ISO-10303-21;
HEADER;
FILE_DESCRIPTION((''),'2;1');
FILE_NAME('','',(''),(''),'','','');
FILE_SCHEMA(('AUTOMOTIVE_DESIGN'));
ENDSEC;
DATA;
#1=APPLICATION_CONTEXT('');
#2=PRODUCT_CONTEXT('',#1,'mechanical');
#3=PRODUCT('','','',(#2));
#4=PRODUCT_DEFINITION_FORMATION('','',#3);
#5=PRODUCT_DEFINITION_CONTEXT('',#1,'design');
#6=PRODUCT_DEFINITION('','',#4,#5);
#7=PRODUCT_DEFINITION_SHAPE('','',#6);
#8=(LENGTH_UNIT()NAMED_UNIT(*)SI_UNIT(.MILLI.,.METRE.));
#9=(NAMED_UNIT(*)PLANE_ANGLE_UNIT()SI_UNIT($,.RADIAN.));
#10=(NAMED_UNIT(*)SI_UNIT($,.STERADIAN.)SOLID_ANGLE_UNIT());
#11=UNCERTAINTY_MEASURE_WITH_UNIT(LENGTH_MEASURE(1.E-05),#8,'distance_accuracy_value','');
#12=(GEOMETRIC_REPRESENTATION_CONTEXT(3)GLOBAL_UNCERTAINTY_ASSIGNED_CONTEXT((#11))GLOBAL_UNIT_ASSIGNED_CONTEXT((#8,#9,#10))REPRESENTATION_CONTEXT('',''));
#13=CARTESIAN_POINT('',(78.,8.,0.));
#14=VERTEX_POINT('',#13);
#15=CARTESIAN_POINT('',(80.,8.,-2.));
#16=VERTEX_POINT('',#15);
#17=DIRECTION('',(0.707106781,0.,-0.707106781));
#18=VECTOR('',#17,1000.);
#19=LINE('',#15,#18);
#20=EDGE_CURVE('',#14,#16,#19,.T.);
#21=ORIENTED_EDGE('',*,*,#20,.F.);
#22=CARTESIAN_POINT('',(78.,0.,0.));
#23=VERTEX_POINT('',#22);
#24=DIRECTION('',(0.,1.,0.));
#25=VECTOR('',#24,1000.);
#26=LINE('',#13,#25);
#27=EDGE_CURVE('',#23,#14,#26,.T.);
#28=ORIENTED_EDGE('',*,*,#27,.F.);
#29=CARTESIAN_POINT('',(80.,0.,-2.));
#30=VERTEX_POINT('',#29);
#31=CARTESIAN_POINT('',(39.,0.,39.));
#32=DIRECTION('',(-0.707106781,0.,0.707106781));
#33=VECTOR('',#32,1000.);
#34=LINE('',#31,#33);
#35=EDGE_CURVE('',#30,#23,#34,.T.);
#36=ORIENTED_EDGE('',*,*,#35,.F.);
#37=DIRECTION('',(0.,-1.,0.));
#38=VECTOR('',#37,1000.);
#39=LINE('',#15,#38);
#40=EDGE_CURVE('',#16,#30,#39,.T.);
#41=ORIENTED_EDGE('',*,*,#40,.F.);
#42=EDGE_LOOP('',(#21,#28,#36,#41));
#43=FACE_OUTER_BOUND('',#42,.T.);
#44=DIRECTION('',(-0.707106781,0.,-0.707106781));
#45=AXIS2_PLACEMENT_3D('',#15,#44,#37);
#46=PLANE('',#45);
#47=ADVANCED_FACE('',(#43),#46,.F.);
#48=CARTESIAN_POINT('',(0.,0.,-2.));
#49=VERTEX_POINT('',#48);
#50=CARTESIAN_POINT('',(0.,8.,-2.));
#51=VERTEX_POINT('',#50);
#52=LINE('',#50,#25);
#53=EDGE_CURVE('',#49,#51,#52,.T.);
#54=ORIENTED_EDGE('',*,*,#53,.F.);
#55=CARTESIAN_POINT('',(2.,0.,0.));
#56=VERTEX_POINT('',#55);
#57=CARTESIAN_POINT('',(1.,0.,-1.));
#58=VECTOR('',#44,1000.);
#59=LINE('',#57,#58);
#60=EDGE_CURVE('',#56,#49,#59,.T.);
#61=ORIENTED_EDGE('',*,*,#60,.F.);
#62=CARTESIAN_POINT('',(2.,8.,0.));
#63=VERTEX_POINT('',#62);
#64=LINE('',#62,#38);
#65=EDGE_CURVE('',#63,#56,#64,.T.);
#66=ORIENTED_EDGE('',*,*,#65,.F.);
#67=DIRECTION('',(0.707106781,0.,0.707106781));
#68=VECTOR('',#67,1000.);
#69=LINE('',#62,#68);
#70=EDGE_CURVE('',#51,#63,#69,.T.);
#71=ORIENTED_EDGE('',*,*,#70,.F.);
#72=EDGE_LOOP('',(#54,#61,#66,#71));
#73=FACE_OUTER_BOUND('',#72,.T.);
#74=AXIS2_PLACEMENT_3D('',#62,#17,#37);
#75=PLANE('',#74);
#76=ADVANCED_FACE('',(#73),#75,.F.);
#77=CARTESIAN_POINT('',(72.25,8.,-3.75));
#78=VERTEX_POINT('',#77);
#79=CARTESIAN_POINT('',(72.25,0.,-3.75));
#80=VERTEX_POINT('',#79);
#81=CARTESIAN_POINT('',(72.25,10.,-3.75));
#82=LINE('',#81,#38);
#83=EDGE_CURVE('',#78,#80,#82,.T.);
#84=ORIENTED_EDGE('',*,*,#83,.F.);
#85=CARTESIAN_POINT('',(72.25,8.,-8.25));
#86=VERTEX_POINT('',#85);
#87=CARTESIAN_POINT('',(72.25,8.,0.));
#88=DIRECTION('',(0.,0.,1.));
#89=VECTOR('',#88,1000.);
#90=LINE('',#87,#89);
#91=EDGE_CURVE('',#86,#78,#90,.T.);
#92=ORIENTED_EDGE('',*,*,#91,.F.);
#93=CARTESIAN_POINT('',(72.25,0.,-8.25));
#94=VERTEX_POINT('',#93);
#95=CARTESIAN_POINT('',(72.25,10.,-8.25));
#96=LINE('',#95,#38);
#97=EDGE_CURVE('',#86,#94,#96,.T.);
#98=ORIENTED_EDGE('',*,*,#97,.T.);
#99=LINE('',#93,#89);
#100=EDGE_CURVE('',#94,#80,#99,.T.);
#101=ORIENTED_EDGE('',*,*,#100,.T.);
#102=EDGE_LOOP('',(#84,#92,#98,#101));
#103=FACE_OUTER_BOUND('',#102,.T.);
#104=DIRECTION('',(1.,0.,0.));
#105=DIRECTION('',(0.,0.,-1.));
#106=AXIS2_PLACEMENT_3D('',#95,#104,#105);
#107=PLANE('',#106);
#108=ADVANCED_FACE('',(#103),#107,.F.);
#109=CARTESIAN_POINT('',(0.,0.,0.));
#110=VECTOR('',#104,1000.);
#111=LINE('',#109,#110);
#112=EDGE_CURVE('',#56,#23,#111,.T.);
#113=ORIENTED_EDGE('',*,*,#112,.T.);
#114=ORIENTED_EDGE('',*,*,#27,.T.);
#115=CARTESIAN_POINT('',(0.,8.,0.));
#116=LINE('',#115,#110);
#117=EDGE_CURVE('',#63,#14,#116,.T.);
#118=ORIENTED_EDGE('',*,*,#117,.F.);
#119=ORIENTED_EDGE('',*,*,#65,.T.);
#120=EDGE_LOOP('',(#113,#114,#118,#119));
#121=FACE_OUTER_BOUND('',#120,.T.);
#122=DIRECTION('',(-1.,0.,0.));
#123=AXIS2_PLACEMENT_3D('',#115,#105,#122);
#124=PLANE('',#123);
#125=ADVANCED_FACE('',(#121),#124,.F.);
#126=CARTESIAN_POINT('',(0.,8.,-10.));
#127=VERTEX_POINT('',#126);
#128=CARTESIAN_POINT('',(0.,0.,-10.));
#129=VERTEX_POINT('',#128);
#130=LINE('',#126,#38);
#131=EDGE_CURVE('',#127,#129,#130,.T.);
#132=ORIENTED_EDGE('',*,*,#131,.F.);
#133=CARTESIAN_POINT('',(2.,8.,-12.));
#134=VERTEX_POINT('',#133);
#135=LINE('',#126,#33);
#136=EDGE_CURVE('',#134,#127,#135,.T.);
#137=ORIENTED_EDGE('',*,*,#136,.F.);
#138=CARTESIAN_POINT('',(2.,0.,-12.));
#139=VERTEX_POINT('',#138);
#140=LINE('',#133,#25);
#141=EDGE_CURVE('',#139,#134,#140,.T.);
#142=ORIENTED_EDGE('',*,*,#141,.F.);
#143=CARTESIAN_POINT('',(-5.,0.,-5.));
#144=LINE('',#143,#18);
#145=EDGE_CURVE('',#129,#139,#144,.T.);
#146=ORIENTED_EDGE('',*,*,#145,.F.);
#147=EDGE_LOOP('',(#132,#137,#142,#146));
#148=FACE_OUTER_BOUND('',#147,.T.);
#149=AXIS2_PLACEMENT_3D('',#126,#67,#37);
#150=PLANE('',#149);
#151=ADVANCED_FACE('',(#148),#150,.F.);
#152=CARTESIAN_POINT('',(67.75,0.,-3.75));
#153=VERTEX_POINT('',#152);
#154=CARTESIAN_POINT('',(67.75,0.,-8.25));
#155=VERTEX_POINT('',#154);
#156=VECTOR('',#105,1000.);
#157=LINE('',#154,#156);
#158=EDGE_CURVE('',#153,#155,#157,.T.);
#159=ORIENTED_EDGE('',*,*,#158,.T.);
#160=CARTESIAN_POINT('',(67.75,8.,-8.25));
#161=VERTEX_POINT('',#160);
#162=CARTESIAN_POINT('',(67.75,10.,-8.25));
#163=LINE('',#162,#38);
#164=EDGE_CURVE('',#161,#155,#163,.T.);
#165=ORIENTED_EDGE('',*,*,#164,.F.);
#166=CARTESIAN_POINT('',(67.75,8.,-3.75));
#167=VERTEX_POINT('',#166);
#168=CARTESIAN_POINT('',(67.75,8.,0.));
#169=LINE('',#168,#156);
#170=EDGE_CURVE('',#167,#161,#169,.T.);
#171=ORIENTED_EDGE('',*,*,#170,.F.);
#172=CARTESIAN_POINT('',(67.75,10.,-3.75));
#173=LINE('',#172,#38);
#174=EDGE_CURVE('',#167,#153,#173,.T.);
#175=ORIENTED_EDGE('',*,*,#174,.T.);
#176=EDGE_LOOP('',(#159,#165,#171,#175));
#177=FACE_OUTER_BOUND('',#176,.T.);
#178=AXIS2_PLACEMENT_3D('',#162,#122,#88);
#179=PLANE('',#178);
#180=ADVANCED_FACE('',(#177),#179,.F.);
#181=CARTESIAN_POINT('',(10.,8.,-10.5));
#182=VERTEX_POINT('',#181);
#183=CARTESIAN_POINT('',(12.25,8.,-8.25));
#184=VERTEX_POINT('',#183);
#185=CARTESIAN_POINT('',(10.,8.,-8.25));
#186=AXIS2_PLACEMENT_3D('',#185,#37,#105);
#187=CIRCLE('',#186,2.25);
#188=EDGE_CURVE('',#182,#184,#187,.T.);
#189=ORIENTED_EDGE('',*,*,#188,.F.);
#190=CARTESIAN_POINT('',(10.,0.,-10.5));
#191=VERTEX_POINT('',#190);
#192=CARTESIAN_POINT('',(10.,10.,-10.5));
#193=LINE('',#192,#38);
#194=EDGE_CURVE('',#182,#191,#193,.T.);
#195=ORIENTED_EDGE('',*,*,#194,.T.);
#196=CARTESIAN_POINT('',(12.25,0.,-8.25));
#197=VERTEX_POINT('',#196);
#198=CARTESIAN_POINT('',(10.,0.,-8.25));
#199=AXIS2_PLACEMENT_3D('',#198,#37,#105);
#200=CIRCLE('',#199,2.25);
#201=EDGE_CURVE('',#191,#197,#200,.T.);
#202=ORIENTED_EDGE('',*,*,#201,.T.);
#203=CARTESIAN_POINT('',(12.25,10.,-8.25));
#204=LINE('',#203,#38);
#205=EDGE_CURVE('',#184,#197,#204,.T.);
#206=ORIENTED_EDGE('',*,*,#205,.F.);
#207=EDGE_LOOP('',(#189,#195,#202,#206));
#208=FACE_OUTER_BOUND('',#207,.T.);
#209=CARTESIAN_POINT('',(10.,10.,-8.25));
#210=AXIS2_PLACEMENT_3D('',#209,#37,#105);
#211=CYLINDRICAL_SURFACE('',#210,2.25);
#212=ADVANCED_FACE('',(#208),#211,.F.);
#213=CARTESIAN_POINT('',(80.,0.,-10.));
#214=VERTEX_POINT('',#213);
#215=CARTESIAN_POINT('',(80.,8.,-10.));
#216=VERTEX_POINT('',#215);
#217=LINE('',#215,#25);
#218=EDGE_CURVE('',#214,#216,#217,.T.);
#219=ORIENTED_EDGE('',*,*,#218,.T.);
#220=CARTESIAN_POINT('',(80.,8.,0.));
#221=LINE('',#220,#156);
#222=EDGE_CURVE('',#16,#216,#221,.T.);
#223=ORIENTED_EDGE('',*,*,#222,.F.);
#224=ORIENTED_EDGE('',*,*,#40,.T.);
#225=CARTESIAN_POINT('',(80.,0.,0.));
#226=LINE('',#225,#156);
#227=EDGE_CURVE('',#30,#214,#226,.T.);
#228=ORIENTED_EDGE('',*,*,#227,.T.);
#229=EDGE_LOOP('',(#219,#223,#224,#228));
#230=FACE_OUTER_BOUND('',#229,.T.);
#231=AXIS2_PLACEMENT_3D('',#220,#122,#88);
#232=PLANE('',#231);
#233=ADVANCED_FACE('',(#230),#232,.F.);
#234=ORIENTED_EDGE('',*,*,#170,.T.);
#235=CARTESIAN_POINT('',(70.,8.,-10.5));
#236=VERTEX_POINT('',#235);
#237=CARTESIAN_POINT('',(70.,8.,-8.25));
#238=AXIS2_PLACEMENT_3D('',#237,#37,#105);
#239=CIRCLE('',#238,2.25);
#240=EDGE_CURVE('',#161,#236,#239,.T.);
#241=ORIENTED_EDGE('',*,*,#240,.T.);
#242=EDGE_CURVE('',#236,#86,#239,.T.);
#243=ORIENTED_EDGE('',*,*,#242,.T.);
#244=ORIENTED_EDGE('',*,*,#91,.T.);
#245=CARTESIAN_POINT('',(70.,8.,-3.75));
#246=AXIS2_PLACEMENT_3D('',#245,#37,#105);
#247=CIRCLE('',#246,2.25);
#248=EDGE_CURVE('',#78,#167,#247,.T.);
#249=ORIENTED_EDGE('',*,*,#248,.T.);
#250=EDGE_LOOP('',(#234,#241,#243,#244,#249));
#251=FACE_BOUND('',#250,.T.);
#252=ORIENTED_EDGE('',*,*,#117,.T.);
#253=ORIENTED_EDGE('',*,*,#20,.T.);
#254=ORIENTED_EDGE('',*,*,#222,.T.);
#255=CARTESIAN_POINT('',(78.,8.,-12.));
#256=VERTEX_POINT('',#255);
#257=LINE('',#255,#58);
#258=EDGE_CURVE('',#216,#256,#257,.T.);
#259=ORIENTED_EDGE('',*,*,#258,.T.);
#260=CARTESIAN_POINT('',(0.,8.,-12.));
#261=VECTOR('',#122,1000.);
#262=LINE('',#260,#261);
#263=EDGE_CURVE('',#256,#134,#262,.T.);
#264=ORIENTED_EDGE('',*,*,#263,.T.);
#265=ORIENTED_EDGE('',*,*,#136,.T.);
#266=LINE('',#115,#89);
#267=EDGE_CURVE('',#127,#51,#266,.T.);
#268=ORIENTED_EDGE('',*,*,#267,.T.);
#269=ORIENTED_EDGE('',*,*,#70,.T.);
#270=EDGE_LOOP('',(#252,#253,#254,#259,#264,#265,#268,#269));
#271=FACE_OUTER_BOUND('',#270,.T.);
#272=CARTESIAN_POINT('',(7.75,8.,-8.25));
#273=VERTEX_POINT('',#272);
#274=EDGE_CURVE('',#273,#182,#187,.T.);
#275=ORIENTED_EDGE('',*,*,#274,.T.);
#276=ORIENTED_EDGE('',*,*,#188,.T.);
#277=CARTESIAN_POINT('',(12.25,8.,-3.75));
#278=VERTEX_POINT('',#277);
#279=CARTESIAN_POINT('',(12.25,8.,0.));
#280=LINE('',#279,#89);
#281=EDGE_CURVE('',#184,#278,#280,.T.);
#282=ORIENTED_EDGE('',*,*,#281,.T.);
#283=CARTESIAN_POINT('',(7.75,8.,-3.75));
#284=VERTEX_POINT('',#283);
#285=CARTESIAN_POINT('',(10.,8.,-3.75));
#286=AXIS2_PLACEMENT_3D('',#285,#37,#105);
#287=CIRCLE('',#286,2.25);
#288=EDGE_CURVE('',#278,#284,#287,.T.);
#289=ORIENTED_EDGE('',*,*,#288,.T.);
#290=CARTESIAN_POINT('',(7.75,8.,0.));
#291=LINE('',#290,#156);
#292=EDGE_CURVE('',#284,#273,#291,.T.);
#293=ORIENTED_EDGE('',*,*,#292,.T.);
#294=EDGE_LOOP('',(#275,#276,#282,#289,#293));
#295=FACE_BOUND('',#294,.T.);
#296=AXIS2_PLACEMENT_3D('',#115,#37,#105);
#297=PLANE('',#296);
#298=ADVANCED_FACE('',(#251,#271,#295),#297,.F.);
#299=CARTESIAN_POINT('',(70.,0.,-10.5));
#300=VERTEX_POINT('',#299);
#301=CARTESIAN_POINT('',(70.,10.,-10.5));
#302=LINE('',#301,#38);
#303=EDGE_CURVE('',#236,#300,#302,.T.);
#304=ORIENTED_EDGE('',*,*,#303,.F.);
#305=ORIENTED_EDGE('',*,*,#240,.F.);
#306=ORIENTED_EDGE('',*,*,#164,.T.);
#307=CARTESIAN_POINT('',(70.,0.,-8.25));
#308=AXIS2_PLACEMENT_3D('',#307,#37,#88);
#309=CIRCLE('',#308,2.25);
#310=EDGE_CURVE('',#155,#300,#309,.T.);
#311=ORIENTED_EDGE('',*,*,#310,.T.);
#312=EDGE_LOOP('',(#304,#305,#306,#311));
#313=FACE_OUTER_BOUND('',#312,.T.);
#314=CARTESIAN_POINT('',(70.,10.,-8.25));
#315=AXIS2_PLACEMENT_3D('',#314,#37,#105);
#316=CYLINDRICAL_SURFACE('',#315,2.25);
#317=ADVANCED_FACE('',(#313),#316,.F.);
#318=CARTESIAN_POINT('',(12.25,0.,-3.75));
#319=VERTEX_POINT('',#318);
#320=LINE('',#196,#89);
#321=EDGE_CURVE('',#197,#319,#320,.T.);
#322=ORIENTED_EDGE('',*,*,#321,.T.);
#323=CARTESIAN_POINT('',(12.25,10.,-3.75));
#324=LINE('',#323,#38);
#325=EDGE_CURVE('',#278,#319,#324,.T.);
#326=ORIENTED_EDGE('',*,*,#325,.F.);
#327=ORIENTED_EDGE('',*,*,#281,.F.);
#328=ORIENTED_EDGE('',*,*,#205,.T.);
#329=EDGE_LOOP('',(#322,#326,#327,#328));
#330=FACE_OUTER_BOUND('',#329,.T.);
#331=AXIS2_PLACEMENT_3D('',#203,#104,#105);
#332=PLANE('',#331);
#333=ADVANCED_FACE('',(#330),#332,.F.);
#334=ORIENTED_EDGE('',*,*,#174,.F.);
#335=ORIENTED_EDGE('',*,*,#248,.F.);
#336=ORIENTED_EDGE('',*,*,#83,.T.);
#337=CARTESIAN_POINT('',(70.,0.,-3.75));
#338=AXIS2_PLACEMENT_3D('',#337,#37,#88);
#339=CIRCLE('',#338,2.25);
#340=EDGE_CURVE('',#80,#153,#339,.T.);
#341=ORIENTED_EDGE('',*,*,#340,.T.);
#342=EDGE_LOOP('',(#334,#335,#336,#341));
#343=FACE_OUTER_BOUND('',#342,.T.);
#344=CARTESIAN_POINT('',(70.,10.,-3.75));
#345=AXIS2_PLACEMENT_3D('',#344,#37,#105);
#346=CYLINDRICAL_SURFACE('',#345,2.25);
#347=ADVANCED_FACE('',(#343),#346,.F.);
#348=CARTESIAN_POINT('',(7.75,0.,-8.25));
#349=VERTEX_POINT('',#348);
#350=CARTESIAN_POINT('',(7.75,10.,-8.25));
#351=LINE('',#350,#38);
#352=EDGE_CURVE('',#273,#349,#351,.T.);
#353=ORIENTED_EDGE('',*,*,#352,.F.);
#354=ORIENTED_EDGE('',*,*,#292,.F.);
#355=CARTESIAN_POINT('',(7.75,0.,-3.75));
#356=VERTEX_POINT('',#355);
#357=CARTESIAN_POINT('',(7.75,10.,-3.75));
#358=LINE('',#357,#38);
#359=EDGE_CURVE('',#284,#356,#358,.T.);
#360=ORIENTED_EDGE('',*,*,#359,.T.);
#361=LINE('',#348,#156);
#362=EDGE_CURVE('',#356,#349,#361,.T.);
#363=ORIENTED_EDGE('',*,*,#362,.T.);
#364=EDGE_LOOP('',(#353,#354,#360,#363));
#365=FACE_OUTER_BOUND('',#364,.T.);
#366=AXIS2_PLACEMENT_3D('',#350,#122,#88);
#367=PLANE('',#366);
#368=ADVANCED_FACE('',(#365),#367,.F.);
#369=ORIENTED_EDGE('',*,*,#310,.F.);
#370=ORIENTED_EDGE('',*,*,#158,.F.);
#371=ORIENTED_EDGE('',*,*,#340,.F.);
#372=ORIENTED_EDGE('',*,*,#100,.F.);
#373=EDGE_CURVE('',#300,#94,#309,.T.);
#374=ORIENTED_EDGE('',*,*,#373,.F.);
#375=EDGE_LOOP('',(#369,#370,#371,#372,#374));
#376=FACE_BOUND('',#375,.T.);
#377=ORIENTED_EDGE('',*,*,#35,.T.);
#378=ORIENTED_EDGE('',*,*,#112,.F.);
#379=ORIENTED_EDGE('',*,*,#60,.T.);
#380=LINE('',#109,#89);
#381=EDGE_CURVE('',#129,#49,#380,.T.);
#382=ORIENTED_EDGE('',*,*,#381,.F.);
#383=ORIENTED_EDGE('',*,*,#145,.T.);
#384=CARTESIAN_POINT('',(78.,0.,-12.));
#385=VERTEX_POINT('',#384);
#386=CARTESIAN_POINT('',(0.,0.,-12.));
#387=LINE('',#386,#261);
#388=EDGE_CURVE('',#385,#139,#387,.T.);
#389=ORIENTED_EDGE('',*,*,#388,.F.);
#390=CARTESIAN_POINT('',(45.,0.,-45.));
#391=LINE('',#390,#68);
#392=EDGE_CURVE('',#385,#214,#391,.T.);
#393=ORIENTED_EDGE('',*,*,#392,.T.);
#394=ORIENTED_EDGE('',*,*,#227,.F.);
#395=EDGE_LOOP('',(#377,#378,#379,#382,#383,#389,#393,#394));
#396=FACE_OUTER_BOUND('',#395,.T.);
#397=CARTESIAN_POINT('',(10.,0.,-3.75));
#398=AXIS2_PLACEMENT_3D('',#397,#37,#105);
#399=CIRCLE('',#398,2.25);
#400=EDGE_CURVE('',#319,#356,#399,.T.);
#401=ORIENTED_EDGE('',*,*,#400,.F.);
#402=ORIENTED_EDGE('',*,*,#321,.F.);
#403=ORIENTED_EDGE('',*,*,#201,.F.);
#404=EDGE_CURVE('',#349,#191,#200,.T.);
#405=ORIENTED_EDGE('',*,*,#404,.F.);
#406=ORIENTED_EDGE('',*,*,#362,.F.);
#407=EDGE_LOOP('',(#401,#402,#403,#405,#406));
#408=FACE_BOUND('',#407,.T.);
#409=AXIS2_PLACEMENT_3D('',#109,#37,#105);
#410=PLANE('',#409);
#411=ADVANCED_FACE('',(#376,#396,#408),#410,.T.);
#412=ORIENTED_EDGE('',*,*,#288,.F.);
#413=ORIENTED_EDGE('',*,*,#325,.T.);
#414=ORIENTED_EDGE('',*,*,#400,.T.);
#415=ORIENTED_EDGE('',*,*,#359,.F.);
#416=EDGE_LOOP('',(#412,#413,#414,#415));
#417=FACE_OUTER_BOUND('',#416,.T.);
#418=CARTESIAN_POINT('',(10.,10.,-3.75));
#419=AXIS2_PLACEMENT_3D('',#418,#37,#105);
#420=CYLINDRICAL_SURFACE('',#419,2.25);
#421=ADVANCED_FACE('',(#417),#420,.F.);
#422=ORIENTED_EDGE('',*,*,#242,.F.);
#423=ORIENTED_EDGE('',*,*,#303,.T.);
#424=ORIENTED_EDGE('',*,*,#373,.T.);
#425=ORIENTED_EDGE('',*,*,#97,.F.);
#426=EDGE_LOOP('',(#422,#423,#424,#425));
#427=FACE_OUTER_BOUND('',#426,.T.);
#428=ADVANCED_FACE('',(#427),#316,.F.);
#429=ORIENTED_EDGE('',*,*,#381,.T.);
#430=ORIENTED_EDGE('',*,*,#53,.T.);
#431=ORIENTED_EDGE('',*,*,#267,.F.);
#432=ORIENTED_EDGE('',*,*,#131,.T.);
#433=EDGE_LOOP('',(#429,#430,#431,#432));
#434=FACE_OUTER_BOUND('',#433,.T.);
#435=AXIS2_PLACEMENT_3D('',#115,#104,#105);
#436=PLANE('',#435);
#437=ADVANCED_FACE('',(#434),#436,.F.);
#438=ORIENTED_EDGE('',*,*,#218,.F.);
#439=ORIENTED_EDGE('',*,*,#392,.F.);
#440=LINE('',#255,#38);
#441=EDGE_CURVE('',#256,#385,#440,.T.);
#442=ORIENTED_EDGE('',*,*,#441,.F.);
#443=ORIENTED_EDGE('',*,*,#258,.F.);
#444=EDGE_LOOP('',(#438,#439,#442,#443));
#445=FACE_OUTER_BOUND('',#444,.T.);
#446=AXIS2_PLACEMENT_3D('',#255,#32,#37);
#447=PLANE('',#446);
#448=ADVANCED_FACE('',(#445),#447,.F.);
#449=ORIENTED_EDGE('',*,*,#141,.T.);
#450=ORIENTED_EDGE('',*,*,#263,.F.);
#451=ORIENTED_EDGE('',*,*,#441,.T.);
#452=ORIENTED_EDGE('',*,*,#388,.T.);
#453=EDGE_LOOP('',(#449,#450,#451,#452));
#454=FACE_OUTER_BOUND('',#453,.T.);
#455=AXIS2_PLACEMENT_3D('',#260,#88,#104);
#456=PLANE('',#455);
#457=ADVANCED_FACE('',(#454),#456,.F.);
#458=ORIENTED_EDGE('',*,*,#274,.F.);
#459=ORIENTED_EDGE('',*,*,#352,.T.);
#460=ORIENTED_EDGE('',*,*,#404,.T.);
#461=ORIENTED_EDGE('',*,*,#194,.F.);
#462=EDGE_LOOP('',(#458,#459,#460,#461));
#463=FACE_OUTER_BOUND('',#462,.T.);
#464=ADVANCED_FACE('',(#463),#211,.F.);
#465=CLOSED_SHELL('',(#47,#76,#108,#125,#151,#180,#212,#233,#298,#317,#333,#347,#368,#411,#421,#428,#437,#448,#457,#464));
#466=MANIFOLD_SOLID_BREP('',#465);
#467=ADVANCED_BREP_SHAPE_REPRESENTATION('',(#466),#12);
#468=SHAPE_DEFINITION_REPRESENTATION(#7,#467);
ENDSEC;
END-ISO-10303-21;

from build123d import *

# Parameters (mm, degrees)
SKETCH1_W           = 80
SKETCH1_H           = 12
BOSS_EXTRUDE1_DEPTH = 8
CHAMFER1_SIZE       = 2
SKETCH2_R           = 2.25
CUT_EXTRUDE1_DEPTH  = 10
CUT_EXTRUDE2_DEPTH  = 10


with BuildPart() as part:
    # Sketch1 → Boss-Extrude1 (new body)
    with BuildSketch(Plane(origin=(0, 0, 0), x_dir=(1, 0, 0), z_dir=(0, 1, 0))):
        with Locations((40, 6)):
            Rectangle(SKETCH1_W, SKETCH1_H)
    extrude(amount=BOSS_EXTRUDE1_DEPTH)

    # Chamfer1
    chamfer1_edges = [part.edges().sort_by_distance(p)[0] for p in [
        (0, 4, -12),
        (80, 4, -12),
        (80, 4, 0),
        (0, 4, 0),
    ]]
    chamfer(chamfer1_edges, length=CHAMFER1_SIZE)

    # Sketch2 → Cut-Extrude1 (cut)
    with BuildSketch(Plane.XZ):
        with Locations(Location((10, -6, 0), (0, 0, 270))):
            Circle(SKETCH2_R)
        with Locations(Location((70, -6, 0), (0, 0, 270))):
            Circle(SKETCH2_R)
    extrude(amount=-CUT_EXTRUDE1_DEPTH, mode=Mode.SUBTRACT)

    # Sketch4 → Cut-Extrude2 (cut)
    with BuildSketch(Plane.XZ):
        with BuildLine():
            Line((7.75, -8.25), (7.75, -3.75))
            ThreePointArc((7.75, -3.75), (10, -1.5), (12.25, -3.75))
            Line((12.25, -3.75), (12.25, -8.25))
            ThreePointArc((12.25, -8.25), (10, -10.5), (7.75, -8.25))
        make_face()
        with BuildLine():
            Line((72.25, -8.25), (72.25, -3.75))
            ThreePointArc((72.25, -3.75), (70, -1.5), (67.75, -3.75))
            Line((67.75, -3.75), (67.75, -8.25))
            ThreePointArc((67.75, -8.25), (70, -10.5), (72.25, -8.25))
        make_face()
    extrude(amount=-CUT_EXTRUDE2_DEPTH, mode=Mode.SUBTRACT)


solid = part.part
